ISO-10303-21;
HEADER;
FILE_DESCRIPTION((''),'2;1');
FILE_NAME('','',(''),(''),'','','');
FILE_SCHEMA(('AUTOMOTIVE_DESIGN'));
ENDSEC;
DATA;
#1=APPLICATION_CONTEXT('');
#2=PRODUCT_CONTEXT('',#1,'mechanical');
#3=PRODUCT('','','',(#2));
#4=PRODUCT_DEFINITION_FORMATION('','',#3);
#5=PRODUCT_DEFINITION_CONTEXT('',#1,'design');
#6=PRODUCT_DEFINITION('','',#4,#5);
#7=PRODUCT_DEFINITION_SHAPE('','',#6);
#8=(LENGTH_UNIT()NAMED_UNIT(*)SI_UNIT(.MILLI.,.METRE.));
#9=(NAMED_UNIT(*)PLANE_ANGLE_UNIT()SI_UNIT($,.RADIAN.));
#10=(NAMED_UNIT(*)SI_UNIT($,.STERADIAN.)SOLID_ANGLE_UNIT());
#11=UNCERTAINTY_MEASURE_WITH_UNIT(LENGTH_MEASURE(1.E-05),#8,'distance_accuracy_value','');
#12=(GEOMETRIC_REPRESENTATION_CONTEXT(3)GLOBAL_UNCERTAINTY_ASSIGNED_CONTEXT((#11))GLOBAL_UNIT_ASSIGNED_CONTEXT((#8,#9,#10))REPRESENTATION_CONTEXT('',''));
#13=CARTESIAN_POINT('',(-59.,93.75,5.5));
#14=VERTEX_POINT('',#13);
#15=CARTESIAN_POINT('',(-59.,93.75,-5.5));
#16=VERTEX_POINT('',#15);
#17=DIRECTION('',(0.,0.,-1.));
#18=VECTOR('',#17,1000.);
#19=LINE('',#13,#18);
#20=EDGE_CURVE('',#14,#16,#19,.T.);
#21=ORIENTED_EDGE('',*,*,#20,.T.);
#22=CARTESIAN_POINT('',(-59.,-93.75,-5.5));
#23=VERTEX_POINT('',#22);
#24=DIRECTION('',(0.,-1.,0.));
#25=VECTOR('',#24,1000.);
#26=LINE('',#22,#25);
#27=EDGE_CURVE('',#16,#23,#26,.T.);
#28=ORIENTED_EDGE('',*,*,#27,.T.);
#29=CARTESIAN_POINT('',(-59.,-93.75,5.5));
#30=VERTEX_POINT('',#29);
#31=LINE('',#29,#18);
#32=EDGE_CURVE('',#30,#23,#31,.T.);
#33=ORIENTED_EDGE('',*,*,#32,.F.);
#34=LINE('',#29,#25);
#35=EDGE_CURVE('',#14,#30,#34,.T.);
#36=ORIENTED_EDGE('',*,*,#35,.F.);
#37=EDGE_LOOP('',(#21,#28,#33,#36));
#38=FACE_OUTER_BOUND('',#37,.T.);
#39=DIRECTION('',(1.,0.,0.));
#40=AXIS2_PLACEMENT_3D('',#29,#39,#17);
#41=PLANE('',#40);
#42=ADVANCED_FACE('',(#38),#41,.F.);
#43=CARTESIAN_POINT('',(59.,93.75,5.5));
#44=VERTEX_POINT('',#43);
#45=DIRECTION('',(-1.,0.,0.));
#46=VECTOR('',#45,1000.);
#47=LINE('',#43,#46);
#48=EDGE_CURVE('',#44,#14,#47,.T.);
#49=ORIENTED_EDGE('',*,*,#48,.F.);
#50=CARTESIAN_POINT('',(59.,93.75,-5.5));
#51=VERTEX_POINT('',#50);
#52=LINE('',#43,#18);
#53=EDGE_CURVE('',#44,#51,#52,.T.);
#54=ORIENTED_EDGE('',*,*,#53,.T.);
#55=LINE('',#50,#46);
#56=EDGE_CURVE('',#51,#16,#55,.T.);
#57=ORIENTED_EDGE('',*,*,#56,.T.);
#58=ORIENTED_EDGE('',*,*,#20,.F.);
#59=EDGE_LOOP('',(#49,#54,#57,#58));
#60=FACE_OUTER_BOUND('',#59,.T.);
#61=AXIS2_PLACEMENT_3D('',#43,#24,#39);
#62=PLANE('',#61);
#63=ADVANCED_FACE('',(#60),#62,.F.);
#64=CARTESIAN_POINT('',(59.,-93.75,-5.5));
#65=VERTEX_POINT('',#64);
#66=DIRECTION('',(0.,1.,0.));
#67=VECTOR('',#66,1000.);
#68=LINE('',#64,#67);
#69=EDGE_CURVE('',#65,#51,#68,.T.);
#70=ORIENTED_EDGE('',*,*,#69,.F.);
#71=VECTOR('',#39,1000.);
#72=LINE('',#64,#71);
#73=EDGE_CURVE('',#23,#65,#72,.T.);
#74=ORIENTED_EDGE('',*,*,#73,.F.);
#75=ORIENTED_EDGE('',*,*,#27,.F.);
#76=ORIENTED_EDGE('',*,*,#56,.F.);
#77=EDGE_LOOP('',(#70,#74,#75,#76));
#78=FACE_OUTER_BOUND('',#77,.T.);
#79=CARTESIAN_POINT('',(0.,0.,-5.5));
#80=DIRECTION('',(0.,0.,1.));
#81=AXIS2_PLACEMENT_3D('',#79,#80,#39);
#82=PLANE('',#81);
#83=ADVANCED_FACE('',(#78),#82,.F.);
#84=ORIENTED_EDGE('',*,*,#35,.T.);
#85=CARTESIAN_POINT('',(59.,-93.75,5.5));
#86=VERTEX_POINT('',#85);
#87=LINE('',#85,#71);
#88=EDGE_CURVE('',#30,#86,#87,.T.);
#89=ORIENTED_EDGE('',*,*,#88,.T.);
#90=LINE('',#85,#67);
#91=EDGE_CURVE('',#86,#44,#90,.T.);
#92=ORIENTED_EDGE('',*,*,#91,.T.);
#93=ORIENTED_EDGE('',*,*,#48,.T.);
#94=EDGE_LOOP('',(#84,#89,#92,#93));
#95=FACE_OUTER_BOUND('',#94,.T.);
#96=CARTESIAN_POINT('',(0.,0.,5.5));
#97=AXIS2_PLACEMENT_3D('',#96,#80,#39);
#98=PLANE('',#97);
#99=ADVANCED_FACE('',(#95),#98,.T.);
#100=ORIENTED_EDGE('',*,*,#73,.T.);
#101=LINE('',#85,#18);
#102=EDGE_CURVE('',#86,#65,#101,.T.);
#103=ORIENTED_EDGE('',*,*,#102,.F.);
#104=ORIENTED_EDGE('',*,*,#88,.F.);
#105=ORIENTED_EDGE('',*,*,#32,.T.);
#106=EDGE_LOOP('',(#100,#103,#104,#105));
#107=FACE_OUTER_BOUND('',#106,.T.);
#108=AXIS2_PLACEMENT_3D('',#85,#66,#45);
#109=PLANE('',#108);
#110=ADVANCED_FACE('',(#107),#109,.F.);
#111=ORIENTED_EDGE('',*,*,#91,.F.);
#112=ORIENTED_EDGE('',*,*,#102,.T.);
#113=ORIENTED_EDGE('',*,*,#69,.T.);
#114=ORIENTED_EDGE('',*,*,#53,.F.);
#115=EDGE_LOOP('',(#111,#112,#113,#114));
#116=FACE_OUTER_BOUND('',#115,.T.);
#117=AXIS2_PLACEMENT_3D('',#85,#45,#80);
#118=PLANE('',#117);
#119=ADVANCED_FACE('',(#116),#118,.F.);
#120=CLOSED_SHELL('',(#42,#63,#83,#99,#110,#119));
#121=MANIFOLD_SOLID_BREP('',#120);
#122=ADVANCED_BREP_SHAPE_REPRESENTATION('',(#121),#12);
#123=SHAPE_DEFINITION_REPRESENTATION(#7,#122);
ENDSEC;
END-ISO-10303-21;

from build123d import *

# Parameters (mm, degrees)
SKETCH1_W           = 118
SKETCH1_H           = 187.5
BOSS_EXTRUDE1_DEPTH = 5.5


with BuildPart() as part:
    # Sketch1 → Boss-Extrude1 (new, symmetric)
    with BuildSketch(Plane.XY):
        Rectangle(SKETCH1_W, SKETCH1_H)
    extrude(amount=BOSS_EXTRUDE1_DEPTH, both=True)


solid = part.part
